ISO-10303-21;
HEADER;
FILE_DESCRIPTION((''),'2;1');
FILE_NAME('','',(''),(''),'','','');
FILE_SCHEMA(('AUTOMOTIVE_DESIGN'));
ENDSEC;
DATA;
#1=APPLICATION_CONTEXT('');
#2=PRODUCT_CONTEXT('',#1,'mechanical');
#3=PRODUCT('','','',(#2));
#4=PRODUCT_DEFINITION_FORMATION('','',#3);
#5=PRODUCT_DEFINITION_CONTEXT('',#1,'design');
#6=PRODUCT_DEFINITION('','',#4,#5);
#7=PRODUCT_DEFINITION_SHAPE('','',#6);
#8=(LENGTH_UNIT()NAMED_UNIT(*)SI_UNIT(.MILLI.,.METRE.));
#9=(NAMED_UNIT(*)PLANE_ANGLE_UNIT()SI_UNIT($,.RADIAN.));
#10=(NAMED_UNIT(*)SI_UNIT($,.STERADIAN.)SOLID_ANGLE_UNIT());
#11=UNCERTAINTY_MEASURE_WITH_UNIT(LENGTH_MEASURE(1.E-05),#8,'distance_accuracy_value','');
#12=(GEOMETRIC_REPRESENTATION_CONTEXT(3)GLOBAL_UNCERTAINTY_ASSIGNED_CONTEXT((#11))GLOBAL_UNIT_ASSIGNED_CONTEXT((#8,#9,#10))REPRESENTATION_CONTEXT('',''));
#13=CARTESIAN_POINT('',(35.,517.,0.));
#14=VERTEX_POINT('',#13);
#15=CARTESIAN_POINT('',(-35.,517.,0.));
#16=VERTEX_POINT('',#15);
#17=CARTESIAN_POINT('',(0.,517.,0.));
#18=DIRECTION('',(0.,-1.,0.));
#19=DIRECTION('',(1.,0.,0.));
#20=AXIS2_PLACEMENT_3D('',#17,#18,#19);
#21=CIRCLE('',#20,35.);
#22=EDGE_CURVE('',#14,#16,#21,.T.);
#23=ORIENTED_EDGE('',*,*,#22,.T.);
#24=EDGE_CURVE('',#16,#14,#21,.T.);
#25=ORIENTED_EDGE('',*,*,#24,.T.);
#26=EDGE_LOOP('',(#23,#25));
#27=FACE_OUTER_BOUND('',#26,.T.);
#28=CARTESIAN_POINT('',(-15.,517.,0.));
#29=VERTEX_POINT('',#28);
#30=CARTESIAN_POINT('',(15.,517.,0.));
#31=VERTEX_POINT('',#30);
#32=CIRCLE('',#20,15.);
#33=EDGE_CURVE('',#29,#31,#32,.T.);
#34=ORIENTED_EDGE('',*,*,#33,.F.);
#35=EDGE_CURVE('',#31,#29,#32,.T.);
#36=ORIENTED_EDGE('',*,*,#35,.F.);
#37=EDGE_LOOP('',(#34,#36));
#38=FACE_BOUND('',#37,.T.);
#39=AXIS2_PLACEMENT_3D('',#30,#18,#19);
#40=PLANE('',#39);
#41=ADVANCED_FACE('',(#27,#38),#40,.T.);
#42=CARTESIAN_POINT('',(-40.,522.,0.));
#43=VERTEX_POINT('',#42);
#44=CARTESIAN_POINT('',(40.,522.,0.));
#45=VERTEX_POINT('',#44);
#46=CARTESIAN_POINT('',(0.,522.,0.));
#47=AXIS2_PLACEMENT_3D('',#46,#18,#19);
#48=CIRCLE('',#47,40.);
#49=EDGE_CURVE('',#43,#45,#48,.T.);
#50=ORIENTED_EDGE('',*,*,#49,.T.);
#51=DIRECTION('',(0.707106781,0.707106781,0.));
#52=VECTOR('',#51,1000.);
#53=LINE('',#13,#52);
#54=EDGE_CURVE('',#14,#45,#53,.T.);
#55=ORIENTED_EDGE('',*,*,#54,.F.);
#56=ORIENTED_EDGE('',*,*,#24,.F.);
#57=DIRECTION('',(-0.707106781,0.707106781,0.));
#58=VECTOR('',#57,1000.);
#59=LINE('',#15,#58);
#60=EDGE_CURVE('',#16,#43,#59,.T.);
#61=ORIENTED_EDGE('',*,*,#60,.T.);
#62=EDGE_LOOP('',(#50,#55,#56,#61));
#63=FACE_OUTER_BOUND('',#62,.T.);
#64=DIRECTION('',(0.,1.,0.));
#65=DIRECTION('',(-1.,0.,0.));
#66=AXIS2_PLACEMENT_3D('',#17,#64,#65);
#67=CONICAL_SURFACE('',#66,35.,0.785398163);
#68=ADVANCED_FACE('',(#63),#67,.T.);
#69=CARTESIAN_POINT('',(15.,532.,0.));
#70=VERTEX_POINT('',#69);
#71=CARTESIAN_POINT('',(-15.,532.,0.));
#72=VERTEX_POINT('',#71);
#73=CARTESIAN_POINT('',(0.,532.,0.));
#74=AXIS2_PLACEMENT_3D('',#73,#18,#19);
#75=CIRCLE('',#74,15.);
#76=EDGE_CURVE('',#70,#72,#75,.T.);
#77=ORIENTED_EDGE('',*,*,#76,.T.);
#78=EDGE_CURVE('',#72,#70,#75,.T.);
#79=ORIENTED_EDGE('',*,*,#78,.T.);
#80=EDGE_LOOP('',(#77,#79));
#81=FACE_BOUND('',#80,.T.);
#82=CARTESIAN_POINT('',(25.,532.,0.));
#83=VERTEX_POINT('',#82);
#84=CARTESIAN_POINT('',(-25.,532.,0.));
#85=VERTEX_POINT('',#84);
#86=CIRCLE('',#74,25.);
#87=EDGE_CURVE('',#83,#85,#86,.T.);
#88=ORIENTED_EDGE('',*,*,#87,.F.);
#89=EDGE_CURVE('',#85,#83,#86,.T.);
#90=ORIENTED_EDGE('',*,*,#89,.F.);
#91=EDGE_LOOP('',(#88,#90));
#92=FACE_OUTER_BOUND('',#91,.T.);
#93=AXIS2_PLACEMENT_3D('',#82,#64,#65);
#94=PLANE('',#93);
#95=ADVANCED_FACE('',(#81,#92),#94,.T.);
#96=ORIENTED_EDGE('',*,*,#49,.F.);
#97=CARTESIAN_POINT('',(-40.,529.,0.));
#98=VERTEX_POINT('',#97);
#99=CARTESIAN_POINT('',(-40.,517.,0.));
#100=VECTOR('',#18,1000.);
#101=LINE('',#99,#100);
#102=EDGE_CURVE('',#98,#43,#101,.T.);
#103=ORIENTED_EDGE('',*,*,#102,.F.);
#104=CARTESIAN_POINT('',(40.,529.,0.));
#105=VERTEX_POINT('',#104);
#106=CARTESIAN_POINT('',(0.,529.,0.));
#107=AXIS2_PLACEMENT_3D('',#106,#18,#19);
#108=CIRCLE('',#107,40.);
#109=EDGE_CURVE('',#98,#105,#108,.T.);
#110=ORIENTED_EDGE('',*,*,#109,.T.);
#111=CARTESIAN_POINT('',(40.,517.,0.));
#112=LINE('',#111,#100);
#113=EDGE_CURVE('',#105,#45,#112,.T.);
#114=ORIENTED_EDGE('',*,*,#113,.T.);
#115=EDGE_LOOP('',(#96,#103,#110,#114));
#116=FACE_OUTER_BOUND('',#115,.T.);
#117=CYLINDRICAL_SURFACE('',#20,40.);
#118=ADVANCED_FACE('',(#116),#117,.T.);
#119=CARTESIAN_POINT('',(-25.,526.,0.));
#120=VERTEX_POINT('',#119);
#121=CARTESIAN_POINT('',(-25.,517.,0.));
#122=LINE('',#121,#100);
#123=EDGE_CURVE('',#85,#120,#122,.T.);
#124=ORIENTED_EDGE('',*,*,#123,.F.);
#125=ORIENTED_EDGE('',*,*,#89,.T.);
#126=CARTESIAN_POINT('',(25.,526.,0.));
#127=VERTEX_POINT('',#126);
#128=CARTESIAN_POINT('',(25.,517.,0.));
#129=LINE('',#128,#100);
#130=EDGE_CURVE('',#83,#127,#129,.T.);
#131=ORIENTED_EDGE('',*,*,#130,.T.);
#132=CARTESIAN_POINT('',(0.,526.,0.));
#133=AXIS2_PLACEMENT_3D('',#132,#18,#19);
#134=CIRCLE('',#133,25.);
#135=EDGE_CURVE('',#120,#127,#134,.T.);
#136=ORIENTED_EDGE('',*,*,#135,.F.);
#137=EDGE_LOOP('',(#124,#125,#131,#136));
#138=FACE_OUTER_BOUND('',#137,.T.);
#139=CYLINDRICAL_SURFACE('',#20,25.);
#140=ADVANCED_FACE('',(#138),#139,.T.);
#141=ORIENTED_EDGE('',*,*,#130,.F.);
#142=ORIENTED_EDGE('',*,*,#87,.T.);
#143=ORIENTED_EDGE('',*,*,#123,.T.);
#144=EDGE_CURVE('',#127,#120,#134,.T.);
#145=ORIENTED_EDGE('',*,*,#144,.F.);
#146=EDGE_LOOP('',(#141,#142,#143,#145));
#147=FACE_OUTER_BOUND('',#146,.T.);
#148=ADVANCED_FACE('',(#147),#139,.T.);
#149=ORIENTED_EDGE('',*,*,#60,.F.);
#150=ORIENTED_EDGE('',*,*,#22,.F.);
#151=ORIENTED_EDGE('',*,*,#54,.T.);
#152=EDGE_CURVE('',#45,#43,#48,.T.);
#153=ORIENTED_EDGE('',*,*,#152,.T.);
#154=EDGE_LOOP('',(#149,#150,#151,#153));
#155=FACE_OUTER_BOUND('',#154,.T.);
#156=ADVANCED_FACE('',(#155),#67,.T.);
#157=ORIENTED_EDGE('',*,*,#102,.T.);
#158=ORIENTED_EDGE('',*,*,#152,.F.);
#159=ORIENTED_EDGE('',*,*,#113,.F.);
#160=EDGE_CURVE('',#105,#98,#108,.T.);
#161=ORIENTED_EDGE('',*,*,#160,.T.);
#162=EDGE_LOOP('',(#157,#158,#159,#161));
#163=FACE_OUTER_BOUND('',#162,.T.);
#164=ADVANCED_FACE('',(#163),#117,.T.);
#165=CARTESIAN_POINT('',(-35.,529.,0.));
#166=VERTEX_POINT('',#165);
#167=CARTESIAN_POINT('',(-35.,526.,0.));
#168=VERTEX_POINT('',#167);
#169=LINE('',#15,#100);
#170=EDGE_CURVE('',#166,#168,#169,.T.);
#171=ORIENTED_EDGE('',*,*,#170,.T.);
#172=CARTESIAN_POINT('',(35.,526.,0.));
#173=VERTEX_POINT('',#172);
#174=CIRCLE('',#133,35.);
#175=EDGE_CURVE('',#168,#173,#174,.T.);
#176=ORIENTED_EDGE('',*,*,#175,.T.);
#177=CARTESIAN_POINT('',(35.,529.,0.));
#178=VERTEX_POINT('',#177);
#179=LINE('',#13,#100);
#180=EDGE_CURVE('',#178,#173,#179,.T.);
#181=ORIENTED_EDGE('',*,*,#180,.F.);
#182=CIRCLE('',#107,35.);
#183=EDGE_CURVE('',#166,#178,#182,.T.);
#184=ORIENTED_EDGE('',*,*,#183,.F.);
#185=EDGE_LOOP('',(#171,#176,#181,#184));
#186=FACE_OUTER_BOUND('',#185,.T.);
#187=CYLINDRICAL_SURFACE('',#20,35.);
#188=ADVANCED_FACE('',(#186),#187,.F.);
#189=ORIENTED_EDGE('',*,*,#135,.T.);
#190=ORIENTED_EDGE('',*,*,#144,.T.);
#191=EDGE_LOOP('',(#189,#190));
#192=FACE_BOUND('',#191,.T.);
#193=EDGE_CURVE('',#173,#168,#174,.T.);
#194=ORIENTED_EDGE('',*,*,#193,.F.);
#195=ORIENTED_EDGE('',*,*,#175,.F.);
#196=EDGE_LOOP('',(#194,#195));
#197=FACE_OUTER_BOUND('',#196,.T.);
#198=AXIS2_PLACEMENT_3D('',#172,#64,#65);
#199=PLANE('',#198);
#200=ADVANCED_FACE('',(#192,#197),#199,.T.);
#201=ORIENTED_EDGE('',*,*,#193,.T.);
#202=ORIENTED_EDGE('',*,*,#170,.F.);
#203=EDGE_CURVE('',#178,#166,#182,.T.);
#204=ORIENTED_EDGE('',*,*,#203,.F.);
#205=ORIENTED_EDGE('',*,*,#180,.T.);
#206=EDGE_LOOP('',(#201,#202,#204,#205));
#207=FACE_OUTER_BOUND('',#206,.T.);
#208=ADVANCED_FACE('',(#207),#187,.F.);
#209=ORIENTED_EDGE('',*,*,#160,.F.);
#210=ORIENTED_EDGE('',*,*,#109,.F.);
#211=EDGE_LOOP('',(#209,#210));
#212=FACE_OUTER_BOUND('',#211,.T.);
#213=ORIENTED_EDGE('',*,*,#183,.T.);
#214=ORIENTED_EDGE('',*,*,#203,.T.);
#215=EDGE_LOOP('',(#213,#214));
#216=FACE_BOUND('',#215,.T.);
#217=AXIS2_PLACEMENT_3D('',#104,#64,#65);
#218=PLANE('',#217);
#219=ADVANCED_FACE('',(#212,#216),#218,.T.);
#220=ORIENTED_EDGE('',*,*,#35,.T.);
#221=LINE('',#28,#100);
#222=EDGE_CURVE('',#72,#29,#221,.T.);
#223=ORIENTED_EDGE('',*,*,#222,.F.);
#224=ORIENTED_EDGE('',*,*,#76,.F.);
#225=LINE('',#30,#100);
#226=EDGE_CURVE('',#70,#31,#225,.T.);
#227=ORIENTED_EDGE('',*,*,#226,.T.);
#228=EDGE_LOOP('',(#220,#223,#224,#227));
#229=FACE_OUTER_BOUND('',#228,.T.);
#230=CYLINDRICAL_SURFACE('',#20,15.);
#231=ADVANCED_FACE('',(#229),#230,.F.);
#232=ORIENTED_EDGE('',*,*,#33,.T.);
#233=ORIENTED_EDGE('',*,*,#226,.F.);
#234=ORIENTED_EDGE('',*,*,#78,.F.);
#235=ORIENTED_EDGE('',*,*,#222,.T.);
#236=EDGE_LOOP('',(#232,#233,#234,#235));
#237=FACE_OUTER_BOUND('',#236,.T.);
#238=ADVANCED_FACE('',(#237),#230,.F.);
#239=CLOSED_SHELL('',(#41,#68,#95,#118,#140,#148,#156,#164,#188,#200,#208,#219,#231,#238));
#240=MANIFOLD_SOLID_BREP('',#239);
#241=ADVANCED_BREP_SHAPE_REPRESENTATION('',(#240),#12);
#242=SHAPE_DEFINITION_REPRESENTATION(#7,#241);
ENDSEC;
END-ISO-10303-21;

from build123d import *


with BuildPart() as part:
    # Sketch1 → Revolve1 (revolve)
    with BuildSketch(Plane.XY):
        Polygon((15, 517), (35, 517), (40, 522), (40, 529), (35, 529), (35, 526), (25, 526), (25, 532), (15, 532), align=None)
    revolve(axis=Axis((0, 517, 0), (0, 1, 0)))


solid = part.part
